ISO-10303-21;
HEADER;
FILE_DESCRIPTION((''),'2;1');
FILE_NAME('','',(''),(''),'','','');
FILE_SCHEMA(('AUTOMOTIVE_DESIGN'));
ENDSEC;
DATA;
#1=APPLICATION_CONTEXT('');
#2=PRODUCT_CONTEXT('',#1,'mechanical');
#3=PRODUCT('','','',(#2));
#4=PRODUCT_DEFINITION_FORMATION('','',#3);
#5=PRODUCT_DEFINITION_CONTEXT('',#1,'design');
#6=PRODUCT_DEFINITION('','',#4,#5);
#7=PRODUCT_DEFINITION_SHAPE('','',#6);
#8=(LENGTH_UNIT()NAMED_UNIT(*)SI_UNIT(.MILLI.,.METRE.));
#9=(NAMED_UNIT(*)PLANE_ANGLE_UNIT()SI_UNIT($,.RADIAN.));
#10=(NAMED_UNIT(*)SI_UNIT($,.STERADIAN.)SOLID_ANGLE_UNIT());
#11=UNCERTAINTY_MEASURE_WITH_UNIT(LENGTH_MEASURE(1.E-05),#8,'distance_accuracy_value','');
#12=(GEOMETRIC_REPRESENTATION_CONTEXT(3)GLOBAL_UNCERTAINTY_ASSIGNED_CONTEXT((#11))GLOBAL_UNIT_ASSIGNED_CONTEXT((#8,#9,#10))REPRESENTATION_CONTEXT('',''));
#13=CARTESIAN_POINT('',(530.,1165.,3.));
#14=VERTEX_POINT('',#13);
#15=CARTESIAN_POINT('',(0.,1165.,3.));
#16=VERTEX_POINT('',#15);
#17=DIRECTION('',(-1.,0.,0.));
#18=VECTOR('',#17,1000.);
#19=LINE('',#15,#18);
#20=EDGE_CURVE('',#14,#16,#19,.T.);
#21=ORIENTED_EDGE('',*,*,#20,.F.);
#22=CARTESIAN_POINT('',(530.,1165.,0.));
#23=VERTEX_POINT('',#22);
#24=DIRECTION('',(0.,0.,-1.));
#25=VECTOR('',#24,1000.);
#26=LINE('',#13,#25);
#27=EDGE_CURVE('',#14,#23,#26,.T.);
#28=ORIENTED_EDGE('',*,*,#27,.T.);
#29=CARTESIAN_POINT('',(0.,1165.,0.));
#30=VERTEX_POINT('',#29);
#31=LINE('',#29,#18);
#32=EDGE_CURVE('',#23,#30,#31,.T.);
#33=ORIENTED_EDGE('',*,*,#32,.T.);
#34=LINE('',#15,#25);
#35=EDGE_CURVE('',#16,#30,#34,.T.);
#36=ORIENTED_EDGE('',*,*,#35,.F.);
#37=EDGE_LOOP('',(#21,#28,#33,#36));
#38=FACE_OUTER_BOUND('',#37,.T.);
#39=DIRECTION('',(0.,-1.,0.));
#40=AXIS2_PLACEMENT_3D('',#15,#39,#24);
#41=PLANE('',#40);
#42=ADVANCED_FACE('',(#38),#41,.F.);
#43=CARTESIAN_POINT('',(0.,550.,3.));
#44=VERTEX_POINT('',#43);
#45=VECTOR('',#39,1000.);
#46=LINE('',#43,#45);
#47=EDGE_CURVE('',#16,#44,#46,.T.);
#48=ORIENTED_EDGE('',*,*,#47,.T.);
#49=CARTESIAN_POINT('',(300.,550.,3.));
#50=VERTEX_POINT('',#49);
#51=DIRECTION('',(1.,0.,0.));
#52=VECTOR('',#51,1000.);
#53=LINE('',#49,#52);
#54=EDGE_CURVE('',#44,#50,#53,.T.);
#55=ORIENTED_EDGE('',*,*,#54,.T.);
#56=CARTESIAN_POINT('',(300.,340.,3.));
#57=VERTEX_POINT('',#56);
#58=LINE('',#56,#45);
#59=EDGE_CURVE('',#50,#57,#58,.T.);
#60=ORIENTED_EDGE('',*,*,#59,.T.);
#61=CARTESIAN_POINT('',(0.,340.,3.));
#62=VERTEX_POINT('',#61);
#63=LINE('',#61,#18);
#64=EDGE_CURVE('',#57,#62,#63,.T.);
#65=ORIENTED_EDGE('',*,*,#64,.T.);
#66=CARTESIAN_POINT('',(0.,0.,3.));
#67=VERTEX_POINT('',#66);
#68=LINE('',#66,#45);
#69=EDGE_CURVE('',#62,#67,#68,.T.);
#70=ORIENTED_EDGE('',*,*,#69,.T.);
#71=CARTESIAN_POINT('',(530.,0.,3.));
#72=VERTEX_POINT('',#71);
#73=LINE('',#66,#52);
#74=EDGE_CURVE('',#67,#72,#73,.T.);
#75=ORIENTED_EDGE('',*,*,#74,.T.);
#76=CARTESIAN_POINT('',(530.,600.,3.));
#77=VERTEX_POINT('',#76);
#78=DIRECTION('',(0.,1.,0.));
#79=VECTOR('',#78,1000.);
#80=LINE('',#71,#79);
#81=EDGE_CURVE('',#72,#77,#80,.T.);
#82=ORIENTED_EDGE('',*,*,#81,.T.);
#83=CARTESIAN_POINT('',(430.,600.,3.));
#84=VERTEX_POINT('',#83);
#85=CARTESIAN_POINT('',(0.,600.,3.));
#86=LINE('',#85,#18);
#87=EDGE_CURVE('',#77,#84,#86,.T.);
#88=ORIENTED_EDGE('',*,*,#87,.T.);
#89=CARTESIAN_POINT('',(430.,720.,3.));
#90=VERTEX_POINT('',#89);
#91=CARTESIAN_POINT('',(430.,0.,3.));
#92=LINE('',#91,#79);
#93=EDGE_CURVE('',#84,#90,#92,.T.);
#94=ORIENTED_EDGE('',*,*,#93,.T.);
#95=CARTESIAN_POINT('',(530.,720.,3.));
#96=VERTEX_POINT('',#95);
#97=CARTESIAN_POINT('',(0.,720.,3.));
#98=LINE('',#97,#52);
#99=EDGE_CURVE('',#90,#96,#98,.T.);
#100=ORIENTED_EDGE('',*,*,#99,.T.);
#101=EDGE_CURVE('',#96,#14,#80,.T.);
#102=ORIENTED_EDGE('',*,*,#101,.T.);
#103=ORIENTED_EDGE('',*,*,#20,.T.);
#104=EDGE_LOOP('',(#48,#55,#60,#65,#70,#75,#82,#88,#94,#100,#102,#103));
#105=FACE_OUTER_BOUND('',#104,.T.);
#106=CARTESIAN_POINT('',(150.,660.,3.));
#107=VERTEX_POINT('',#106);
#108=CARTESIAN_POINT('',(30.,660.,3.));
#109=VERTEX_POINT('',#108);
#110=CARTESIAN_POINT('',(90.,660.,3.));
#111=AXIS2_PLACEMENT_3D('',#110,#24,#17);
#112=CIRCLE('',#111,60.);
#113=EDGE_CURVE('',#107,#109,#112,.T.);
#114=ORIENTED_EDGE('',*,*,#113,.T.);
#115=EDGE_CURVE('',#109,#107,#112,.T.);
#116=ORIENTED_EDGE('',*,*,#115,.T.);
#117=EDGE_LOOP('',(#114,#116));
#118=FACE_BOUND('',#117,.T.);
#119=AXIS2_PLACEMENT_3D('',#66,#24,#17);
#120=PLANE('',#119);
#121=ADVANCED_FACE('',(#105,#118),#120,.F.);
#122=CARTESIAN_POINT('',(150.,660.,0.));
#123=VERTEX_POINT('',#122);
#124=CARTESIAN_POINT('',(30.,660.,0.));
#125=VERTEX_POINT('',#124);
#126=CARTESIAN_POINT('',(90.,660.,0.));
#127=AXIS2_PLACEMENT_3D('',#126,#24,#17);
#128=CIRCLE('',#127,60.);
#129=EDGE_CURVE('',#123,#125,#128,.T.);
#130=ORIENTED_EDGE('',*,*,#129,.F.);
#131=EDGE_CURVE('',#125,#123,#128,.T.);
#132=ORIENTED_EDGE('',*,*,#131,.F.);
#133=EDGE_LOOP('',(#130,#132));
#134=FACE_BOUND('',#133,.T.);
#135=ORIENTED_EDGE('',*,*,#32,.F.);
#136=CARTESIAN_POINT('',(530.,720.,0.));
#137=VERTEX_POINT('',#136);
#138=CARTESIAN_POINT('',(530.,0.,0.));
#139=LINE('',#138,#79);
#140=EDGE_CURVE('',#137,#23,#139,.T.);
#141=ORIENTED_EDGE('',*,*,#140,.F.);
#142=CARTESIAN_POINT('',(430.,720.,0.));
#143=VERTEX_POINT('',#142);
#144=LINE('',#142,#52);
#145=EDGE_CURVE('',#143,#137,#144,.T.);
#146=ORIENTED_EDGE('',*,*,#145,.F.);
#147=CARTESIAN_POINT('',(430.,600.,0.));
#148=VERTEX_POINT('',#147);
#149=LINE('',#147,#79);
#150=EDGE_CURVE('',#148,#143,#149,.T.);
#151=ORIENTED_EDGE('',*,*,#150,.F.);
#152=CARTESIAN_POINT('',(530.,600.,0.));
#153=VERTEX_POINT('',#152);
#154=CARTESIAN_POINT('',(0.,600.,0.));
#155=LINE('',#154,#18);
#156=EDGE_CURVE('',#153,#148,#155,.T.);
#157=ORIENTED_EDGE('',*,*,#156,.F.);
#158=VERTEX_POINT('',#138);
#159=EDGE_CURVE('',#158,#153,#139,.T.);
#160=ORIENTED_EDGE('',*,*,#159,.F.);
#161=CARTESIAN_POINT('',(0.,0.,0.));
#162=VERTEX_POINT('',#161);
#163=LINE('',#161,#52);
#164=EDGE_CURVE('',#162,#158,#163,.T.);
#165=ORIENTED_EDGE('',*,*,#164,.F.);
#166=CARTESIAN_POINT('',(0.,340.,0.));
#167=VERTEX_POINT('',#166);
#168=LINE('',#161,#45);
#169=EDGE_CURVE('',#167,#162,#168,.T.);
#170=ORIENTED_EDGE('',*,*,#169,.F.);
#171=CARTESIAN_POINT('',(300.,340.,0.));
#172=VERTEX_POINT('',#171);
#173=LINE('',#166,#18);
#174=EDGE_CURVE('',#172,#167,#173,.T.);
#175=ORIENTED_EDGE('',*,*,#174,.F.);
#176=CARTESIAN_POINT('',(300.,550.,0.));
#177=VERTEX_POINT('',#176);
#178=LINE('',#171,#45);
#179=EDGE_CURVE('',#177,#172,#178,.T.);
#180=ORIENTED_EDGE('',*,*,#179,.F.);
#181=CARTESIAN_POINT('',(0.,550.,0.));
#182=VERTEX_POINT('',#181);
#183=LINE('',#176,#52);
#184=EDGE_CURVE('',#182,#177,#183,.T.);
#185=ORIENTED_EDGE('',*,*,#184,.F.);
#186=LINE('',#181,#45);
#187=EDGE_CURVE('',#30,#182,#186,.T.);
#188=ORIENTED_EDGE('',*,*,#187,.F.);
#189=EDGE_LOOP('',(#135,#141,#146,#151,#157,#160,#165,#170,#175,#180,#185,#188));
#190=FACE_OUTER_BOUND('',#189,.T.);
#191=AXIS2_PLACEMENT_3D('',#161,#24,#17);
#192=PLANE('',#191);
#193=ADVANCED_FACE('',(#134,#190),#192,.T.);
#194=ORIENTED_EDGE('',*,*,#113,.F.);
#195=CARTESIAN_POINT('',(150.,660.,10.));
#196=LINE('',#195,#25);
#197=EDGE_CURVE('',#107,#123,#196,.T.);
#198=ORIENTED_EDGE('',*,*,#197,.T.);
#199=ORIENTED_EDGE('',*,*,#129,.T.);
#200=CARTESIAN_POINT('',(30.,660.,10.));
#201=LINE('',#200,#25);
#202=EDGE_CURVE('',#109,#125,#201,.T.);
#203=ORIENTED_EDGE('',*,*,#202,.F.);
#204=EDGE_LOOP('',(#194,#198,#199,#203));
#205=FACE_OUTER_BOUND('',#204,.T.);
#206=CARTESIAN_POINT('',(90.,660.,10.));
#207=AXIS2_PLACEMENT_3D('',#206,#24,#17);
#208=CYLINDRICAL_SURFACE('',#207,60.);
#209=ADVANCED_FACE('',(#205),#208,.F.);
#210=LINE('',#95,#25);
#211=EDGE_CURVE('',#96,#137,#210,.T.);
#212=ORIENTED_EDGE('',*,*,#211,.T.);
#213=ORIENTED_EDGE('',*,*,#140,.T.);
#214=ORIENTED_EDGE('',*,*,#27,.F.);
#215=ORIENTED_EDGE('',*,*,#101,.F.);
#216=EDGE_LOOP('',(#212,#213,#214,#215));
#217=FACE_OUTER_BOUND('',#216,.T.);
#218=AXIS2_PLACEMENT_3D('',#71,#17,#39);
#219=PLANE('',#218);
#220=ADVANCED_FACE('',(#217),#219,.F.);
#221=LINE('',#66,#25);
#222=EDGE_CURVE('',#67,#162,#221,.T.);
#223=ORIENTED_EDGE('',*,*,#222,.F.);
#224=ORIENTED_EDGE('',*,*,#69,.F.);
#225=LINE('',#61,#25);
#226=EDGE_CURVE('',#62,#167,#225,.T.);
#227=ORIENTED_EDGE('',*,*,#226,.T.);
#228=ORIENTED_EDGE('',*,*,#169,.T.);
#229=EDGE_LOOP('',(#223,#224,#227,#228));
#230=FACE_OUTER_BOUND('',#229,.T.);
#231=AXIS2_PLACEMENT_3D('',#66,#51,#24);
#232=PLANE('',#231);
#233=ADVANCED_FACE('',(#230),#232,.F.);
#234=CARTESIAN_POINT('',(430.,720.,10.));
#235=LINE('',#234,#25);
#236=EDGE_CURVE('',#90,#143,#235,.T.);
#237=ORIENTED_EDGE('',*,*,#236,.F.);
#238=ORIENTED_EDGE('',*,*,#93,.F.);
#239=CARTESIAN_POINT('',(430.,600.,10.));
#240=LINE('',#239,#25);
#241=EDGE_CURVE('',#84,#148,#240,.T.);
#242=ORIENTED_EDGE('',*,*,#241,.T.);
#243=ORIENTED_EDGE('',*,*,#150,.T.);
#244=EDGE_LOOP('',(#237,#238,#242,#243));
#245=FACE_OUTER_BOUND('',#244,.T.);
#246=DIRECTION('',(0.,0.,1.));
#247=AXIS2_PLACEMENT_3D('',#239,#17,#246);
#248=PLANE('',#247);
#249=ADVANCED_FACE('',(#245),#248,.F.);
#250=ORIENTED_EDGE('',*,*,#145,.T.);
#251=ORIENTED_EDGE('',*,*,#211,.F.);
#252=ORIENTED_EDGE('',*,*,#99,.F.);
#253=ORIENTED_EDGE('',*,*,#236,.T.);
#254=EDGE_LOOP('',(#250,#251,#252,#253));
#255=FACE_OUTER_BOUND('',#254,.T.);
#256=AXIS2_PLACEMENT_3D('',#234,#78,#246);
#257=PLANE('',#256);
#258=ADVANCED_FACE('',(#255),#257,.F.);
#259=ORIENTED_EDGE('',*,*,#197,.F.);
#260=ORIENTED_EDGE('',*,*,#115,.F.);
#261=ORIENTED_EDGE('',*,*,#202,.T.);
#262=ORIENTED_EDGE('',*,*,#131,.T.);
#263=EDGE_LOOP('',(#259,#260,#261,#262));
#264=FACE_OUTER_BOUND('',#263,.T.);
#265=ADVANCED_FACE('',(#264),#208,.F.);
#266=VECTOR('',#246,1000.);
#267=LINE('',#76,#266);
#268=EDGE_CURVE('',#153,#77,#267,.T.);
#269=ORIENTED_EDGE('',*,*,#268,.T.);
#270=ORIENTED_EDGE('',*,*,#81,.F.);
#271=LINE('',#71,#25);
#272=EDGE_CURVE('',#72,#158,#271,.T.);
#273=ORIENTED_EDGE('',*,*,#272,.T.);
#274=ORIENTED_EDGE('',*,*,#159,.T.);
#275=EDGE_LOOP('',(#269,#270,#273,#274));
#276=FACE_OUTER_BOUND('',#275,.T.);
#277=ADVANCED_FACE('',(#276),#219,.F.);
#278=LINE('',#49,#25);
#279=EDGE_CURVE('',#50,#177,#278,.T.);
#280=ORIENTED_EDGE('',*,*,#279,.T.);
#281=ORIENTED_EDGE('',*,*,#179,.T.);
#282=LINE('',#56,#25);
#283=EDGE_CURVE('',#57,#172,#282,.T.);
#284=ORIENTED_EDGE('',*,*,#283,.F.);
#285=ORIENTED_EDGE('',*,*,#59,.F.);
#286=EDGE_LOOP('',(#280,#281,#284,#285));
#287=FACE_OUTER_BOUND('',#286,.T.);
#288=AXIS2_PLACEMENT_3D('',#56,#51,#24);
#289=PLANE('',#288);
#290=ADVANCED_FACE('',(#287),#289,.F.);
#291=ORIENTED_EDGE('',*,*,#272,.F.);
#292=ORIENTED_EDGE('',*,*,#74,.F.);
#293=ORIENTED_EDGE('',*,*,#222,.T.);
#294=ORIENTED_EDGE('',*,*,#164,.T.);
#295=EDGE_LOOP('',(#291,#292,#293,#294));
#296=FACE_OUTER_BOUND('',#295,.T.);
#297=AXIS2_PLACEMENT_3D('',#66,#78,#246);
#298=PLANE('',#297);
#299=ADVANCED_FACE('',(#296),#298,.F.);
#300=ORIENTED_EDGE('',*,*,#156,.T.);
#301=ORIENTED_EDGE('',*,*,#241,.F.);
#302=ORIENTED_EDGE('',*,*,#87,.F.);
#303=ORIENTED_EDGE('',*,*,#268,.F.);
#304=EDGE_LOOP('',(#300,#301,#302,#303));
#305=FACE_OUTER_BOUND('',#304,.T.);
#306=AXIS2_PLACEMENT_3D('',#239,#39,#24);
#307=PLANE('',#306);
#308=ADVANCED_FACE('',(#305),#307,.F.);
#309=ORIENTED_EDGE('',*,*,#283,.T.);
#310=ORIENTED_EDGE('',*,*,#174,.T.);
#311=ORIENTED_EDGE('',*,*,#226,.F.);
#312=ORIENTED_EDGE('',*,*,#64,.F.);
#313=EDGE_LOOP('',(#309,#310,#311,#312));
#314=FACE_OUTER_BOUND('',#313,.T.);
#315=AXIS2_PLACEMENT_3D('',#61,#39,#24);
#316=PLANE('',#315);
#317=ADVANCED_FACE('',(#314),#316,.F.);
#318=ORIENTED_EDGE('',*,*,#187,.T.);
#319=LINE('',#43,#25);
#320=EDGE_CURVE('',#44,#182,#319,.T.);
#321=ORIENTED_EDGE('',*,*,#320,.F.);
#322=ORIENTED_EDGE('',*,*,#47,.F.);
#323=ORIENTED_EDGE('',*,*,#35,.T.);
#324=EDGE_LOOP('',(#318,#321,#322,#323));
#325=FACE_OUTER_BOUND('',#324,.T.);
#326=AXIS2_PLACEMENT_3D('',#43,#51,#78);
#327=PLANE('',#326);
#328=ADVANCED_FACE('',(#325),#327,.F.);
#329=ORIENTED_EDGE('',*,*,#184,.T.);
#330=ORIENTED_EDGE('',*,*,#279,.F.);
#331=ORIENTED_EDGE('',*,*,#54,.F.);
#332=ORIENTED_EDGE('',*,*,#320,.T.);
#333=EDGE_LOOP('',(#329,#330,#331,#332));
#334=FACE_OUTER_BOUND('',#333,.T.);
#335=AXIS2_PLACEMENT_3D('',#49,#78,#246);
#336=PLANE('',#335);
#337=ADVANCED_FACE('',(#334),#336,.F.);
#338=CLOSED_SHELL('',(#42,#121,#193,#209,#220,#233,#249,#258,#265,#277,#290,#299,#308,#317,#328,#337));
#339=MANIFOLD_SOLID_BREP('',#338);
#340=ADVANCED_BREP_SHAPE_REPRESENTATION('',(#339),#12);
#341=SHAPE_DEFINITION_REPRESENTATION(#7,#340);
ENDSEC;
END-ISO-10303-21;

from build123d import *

# Parameters (mm, degrees)
BOSS_EXTRUDE1_DEPTH = 3
SKETCH2_R           = 60
SKETCH2_W           = 120
SKETCH2_H           = 120
CUT_EXTRUDE1_DEPTH  = 10


with BuildPart() as part:
    # Sketch1 → Boss-Extrude1 (new body)
    with BuildSketch(Plane.XY):
        Polygon((0, 0), (530, 0), (530, 1165), (0, 1165), (0, 550), (300, 550), (300, 340), (0, 340), align=None)
    extrude(amount=BOSS_EXTRUDE1_DEPTH)

    # Sketch2 → Cut-Extrude1 (cut)
    with BuildSketch(Plane(origin=(0, 0, 0), x_dir=(-1, 0, 0), z_dir=(0, 0, -1))):
        with Locations((-90, 660)):
            Circle(SKETCH2_R)
        with Locations((-490, 660)):
            Rectangle(SKETCH2_W, SKETCH2_H)
    extrude(amount=-CUT_EXTRUDE1_DEPTH, mode=Mode.SUBTRACT)


solid = part.part
